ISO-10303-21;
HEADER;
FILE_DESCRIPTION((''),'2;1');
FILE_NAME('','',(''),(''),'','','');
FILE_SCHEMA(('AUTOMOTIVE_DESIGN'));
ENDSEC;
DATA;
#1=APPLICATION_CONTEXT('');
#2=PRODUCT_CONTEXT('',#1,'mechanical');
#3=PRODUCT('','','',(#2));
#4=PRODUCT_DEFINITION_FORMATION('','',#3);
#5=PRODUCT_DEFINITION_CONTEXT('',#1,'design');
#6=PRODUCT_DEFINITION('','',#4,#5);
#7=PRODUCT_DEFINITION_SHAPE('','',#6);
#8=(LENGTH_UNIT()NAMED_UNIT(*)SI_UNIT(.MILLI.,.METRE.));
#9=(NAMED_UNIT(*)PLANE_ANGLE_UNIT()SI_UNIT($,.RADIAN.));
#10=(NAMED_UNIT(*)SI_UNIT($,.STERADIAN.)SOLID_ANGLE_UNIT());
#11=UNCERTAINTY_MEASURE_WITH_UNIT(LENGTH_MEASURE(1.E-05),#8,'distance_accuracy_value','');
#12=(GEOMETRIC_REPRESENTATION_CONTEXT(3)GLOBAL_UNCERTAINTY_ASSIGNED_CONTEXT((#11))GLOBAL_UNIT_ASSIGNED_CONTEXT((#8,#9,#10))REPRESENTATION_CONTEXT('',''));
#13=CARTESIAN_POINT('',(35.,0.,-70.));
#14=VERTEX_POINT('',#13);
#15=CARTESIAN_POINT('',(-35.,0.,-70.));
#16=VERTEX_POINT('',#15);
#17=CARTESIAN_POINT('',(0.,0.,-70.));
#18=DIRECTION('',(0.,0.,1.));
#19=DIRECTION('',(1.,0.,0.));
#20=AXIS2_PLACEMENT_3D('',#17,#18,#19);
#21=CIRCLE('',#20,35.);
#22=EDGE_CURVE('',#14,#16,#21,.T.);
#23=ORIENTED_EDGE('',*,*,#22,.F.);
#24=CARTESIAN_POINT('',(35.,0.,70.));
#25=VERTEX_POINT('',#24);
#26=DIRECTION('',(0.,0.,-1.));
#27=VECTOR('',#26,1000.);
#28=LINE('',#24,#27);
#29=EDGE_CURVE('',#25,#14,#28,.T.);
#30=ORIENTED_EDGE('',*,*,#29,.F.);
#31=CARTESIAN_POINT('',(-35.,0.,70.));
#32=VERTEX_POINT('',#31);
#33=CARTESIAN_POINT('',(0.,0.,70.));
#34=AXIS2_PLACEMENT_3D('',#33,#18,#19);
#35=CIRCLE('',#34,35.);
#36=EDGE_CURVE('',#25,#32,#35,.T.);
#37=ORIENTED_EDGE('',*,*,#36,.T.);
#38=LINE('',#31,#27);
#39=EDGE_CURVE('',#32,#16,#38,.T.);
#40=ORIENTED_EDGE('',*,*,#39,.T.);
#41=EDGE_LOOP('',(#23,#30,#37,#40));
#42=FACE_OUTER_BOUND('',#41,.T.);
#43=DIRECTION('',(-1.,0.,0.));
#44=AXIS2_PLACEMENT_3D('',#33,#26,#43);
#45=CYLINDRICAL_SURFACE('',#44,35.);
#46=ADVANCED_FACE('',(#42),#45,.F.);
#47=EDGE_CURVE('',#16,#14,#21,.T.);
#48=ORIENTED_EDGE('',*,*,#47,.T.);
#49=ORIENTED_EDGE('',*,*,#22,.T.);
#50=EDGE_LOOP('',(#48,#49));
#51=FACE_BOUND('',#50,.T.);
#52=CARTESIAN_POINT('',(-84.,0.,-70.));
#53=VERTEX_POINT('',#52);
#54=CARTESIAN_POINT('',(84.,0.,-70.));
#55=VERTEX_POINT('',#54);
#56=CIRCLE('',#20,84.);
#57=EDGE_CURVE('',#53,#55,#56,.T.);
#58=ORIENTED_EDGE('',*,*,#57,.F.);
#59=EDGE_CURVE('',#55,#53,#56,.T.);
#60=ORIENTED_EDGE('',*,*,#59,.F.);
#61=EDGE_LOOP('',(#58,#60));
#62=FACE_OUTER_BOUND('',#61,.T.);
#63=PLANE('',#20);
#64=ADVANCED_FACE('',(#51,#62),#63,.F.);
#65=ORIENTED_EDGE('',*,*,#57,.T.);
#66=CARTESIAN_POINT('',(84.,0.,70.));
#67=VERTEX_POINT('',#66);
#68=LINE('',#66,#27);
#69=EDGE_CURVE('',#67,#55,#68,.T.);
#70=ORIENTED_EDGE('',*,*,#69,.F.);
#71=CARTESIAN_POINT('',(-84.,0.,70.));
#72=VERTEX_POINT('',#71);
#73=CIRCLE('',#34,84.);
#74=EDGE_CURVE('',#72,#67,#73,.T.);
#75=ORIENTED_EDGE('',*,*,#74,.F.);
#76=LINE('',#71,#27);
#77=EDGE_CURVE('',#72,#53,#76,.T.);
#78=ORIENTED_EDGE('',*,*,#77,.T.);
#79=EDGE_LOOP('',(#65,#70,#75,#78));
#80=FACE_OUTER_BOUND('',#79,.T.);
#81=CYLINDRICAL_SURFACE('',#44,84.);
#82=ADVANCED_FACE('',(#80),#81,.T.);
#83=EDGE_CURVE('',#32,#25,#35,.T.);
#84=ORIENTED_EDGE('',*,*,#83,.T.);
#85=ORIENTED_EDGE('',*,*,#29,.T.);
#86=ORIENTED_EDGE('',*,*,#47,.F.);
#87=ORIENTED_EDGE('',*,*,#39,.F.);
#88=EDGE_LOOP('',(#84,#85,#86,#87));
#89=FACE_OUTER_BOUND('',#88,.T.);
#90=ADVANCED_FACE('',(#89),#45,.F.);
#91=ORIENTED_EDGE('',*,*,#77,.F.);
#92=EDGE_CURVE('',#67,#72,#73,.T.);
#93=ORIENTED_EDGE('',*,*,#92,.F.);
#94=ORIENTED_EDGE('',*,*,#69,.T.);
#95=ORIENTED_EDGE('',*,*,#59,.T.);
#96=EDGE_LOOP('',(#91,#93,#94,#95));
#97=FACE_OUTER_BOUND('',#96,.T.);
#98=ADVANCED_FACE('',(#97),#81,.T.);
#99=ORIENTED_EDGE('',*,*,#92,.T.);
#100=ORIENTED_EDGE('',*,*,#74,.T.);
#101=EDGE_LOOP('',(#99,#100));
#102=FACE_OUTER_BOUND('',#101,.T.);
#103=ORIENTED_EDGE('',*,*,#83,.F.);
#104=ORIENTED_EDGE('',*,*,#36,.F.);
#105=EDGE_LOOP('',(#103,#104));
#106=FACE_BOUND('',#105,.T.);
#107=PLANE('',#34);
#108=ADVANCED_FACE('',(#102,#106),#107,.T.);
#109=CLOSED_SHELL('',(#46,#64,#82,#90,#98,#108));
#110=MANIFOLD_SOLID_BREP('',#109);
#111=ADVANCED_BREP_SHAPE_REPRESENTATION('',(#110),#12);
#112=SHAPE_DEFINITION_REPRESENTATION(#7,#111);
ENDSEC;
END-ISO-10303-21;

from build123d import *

# Parameters (mm, degrees)
SKETCH1_R           = 84
SKETCH1_R_2         = 35
BOSS_EXTRUDE1_DEPTH = 70


with BuildPart() as part:
    # Sketch1 → Boss-Extrude1 (new, symmetric)
    with BuildSketch(Plane.XY):
        Circle(SKETCH1_R)
        Circle(SKETCH1_R_2, mode=Mode.SUBTRACT)
    extrude(amount=BOSS_EXTRUDE1_DEPTH, both=True)


solid = part.part
